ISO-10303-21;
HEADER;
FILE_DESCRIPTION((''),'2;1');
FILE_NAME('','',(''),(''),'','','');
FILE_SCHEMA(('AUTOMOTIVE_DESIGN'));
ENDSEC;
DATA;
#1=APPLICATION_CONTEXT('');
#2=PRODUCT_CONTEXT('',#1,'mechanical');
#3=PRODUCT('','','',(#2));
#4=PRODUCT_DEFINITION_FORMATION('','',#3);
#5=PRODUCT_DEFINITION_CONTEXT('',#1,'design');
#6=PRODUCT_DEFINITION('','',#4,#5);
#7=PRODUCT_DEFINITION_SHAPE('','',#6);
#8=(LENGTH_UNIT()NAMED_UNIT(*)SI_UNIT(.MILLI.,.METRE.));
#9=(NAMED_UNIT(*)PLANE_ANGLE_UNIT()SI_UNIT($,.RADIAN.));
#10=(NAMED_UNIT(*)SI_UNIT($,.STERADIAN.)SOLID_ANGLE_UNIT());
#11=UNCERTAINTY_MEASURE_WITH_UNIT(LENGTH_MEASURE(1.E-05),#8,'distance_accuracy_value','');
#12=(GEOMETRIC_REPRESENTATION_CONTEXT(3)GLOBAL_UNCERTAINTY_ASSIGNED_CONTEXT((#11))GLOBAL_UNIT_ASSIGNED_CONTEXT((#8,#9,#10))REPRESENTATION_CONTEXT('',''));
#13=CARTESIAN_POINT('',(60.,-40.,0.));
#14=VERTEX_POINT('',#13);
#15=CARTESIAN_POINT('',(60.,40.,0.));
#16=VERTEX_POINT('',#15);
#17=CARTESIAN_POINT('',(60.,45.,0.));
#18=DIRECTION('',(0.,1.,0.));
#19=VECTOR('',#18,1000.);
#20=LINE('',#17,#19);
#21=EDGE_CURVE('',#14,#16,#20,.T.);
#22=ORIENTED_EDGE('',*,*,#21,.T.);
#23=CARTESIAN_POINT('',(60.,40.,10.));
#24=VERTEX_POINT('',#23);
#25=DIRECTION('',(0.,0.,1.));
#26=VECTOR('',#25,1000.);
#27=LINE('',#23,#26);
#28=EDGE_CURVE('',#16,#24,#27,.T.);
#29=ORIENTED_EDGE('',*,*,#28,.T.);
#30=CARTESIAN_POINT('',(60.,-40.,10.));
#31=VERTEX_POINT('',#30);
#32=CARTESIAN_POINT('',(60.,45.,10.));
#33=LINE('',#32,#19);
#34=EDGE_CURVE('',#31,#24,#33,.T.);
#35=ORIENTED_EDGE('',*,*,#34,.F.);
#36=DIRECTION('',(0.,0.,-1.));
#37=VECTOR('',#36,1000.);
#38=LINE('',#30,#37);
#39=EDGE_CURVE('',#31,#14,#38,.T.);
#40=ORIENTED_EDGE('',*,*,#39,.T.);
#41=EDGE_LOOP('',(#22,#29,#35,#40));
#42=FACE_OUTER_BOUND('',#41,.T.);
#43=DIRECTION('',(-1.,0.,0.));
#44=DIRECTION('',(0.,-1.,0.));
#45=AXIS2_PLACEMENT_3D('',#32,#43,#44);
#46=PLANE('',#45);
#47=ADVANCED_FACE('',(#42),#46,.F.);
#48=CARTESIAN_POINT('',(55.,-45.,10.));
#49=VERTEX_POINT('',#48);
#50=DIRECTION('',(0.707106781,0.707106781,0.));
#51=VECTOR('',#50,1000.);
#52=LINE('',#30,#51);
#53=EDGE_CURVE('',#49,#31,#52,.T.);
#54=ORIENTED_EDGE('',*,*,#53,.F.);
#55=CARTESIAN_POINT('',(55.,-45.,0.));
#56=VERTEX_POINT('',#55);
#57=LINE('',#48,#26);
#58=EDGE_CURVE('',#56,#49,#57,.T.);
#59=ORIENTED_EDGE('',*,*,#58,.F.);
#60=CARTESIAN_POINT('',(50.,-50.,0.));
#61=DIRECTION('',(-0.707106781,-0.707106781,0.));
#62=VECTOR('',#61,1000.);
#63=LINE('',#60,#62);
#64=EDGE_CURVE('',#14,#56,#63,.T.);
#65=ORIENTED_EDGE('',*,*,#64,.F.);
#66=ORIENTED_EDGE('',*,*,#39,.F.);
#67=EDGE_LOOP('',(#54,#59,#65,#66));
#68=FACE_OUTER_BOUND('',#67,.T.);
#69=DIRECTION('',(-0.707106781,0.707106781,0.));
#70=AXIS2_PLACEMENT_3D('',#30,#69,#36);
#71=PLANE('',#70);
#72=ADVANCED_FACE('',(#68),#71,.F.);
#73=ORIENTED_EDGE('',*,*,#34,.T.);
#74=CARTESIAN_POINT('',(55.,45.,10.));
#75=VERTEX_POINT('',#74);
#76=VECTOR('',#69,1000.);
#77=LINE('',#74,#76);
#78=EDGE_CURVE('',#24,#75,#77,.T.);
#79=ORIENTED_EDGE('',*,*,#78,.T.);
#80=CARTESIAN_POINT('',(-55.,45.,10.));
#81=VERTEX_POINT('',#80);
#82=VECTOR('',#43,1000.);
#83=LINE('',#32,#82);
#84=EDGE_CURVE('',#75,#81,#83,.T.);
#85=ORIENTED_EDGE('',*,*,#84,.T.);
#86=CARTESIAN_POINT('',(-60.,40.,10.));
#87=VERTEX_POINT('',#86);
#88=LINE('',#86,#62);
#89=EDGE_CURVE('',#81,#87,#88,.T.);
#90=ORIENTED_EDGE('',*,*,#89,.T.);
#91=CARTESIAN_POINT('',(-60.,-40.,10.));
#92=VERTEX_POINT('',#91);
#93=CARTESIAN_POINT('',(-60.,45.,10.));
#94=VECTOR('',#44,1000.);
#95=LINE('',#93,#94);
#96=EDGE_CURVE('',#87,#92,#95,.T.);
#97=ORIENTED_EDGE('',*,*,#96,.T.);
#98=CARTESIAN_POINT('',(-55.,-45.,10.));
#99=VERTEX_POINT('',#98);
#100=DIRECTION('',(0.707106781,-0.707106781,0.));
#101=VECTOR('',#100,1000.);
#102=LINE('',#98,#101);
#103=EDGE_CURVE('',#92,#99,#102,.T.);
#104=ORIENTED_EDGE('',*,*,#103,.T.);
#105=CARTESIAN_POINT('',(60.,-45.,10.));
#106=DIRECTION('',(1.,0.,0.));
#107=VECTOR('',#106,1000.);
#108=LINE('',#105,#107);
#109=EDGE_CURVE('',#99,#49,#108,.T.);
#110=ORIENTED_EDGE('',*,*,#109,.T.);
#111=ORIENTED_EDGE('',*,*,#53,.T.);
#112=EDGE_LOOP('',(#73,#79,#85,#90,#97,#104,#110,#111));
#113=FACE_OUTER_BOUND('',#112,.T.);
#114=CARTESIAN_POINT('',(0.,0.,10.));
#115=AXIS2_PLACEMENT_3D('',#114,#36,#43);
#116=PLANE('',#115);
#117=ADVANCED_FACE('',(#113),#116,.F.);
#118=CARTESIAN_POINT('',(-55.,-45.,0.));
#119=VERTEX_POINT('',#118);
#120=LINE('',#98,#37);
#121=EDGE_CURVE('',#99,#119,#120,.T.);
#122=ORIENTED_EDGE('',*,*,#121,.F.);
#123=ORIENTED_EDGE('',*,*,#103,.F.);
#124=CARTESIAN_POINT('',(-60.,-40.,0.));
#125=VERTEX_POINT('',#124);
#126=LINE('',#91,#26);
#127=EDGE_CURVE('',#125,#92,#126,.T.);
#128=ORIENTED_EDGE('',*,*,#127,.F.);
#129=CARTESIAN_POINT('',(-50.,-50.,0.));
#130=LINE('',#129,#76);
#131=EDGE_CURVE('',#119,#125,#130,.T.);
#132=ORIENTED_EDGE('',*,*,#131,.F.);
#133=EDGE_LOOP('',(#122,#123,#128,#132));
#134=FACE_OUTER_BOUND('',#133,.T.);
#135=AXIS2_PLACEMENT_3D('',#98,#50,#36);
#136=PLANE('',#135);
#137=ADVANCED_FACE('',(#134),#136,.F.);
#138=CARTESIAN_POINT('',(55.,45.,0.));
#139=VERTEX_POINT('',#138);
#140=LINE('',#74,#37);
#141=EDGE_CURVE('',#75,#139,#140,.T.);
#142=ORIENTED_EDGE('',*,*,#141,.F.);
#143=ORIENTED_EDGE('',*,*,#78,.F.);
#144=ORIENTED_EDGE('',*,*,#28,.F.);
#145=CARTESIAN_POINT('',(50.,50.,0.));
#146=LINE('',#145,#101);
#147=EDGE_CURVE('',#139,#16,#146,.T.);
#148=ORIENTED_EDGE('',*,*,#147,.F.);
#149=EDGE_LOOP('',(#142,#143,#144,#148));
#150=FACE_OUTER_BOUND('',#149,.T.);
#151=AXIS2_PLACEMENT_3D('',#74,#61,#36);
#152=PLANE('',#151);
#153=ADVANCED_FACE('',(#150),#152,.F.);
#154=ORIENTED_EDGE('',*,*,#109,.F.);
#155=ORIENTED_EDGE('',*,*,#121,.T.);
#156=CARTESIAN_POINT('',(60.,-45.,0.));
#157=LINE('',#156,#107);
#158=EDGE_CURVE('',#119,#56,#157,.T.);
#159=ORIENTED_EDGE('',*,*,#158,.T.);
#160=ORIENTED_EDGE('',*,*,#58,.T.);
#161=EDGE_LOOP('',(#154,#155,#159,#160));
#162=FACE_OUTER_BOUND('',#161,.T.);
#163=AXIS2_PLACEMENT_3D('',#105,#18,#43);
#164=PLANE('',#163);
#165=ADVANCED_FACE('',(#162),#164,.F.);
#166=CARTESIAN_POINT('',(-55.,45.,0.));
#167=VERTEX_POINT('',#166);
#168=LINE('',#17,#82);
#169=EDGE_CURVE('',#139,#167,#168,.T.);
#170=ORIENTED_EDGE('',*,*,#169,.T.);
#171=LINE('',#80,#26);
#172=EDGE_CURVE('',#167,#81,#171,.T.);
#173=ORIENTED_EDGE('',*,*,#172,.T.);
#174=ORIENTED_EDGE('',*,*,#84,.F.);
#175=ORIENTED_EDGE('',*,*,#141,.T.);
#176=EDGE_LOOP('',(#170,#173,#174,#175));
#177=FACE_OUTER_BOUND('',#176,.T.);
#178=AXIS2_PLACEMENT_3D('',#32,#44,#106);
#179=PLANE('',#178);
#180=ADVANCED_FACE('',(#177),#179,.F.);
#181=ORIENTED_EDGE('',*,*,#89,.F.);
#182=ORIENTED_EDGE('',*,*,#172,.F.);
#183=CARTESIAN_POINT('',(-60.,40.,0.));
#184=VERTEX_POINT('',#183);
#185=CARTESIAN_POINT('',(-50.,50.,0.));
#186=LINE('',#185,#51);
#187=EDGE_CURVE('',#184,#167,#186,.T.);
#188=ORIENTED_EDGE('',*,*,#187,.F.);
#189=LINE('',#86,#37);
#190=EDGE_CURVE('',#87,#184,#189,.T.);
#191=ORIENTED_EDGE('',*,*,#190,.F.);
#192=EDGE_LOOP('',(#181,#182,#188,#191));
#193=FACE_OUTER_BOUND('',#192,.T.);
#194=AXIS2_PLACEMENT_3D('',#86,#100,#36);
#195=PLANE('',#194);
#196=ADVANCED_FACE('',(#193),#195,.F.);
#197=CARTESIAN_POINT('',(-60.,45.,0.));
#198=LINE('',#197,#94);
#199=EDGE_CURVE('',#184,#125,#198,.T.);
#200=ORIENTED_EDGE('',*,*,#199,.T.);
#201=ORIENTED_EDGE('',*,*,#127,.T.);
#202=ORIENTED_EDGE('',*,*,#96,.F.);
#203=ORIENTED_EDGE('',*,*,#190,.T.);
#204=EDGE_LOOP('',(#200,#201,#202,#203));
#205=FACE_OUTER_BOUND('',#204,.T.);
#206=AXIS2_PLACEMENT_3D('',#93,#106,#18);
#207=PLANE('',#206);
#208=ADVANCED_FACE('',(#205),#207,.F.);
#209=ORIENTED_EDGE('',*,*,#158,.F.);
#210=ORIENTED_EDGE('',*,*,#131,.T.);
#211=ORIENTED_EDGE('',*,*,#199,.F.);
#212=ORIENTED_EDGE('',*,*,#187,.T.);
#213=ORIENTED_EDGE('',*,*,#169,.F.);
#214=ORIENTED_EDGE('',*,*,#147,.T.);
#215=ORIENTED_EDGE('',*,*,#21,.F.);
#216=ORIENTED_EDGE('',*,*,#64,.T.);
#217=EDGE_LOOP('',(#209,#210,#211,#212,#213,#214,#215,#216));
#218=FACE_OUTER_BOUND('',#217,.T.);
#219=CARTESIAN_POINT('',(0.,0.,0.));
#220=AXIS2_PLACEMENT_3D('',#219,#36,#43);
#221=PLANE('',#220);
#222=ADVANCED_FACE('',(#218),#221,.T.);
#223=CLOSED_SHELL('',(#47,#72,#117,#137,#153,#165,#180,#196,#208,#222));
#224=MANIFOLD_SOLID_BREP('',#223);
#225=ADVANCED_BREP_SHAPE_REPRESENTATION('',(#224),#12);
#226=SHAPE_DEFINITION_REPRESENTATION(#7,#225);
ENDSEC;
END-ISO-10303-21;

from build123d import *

# Parameters (mm, degrees)
SKETCH1_W           = 120
SKETCH1_H           = 90
BOSS_EXTRUDE1_DEPTH = 10
CHAMFER1_SIZE       = 5


with BuildPart() as part:
    # Sketch1 → Boss-Extrude1 (new body)
    with BuildSketch(Plane.XY):
        Rectangle(SKETCH1_W, SKETCH1_H)
    extrude(amount=BOSS_EXTRUDE1_DEPTH)

    # Chamfer1
    chamfer1_edges = [part.edges().sort_by_distance(p)[0] for p in [
        (-60, 45, 5),
        (60, 45, 5),
        (60, -45, 5),
        (-60, -45, 5),
    ]]
    chamfer(chamfer1_edges, length=CHAMFER1_SIZE)


solid = part.part
